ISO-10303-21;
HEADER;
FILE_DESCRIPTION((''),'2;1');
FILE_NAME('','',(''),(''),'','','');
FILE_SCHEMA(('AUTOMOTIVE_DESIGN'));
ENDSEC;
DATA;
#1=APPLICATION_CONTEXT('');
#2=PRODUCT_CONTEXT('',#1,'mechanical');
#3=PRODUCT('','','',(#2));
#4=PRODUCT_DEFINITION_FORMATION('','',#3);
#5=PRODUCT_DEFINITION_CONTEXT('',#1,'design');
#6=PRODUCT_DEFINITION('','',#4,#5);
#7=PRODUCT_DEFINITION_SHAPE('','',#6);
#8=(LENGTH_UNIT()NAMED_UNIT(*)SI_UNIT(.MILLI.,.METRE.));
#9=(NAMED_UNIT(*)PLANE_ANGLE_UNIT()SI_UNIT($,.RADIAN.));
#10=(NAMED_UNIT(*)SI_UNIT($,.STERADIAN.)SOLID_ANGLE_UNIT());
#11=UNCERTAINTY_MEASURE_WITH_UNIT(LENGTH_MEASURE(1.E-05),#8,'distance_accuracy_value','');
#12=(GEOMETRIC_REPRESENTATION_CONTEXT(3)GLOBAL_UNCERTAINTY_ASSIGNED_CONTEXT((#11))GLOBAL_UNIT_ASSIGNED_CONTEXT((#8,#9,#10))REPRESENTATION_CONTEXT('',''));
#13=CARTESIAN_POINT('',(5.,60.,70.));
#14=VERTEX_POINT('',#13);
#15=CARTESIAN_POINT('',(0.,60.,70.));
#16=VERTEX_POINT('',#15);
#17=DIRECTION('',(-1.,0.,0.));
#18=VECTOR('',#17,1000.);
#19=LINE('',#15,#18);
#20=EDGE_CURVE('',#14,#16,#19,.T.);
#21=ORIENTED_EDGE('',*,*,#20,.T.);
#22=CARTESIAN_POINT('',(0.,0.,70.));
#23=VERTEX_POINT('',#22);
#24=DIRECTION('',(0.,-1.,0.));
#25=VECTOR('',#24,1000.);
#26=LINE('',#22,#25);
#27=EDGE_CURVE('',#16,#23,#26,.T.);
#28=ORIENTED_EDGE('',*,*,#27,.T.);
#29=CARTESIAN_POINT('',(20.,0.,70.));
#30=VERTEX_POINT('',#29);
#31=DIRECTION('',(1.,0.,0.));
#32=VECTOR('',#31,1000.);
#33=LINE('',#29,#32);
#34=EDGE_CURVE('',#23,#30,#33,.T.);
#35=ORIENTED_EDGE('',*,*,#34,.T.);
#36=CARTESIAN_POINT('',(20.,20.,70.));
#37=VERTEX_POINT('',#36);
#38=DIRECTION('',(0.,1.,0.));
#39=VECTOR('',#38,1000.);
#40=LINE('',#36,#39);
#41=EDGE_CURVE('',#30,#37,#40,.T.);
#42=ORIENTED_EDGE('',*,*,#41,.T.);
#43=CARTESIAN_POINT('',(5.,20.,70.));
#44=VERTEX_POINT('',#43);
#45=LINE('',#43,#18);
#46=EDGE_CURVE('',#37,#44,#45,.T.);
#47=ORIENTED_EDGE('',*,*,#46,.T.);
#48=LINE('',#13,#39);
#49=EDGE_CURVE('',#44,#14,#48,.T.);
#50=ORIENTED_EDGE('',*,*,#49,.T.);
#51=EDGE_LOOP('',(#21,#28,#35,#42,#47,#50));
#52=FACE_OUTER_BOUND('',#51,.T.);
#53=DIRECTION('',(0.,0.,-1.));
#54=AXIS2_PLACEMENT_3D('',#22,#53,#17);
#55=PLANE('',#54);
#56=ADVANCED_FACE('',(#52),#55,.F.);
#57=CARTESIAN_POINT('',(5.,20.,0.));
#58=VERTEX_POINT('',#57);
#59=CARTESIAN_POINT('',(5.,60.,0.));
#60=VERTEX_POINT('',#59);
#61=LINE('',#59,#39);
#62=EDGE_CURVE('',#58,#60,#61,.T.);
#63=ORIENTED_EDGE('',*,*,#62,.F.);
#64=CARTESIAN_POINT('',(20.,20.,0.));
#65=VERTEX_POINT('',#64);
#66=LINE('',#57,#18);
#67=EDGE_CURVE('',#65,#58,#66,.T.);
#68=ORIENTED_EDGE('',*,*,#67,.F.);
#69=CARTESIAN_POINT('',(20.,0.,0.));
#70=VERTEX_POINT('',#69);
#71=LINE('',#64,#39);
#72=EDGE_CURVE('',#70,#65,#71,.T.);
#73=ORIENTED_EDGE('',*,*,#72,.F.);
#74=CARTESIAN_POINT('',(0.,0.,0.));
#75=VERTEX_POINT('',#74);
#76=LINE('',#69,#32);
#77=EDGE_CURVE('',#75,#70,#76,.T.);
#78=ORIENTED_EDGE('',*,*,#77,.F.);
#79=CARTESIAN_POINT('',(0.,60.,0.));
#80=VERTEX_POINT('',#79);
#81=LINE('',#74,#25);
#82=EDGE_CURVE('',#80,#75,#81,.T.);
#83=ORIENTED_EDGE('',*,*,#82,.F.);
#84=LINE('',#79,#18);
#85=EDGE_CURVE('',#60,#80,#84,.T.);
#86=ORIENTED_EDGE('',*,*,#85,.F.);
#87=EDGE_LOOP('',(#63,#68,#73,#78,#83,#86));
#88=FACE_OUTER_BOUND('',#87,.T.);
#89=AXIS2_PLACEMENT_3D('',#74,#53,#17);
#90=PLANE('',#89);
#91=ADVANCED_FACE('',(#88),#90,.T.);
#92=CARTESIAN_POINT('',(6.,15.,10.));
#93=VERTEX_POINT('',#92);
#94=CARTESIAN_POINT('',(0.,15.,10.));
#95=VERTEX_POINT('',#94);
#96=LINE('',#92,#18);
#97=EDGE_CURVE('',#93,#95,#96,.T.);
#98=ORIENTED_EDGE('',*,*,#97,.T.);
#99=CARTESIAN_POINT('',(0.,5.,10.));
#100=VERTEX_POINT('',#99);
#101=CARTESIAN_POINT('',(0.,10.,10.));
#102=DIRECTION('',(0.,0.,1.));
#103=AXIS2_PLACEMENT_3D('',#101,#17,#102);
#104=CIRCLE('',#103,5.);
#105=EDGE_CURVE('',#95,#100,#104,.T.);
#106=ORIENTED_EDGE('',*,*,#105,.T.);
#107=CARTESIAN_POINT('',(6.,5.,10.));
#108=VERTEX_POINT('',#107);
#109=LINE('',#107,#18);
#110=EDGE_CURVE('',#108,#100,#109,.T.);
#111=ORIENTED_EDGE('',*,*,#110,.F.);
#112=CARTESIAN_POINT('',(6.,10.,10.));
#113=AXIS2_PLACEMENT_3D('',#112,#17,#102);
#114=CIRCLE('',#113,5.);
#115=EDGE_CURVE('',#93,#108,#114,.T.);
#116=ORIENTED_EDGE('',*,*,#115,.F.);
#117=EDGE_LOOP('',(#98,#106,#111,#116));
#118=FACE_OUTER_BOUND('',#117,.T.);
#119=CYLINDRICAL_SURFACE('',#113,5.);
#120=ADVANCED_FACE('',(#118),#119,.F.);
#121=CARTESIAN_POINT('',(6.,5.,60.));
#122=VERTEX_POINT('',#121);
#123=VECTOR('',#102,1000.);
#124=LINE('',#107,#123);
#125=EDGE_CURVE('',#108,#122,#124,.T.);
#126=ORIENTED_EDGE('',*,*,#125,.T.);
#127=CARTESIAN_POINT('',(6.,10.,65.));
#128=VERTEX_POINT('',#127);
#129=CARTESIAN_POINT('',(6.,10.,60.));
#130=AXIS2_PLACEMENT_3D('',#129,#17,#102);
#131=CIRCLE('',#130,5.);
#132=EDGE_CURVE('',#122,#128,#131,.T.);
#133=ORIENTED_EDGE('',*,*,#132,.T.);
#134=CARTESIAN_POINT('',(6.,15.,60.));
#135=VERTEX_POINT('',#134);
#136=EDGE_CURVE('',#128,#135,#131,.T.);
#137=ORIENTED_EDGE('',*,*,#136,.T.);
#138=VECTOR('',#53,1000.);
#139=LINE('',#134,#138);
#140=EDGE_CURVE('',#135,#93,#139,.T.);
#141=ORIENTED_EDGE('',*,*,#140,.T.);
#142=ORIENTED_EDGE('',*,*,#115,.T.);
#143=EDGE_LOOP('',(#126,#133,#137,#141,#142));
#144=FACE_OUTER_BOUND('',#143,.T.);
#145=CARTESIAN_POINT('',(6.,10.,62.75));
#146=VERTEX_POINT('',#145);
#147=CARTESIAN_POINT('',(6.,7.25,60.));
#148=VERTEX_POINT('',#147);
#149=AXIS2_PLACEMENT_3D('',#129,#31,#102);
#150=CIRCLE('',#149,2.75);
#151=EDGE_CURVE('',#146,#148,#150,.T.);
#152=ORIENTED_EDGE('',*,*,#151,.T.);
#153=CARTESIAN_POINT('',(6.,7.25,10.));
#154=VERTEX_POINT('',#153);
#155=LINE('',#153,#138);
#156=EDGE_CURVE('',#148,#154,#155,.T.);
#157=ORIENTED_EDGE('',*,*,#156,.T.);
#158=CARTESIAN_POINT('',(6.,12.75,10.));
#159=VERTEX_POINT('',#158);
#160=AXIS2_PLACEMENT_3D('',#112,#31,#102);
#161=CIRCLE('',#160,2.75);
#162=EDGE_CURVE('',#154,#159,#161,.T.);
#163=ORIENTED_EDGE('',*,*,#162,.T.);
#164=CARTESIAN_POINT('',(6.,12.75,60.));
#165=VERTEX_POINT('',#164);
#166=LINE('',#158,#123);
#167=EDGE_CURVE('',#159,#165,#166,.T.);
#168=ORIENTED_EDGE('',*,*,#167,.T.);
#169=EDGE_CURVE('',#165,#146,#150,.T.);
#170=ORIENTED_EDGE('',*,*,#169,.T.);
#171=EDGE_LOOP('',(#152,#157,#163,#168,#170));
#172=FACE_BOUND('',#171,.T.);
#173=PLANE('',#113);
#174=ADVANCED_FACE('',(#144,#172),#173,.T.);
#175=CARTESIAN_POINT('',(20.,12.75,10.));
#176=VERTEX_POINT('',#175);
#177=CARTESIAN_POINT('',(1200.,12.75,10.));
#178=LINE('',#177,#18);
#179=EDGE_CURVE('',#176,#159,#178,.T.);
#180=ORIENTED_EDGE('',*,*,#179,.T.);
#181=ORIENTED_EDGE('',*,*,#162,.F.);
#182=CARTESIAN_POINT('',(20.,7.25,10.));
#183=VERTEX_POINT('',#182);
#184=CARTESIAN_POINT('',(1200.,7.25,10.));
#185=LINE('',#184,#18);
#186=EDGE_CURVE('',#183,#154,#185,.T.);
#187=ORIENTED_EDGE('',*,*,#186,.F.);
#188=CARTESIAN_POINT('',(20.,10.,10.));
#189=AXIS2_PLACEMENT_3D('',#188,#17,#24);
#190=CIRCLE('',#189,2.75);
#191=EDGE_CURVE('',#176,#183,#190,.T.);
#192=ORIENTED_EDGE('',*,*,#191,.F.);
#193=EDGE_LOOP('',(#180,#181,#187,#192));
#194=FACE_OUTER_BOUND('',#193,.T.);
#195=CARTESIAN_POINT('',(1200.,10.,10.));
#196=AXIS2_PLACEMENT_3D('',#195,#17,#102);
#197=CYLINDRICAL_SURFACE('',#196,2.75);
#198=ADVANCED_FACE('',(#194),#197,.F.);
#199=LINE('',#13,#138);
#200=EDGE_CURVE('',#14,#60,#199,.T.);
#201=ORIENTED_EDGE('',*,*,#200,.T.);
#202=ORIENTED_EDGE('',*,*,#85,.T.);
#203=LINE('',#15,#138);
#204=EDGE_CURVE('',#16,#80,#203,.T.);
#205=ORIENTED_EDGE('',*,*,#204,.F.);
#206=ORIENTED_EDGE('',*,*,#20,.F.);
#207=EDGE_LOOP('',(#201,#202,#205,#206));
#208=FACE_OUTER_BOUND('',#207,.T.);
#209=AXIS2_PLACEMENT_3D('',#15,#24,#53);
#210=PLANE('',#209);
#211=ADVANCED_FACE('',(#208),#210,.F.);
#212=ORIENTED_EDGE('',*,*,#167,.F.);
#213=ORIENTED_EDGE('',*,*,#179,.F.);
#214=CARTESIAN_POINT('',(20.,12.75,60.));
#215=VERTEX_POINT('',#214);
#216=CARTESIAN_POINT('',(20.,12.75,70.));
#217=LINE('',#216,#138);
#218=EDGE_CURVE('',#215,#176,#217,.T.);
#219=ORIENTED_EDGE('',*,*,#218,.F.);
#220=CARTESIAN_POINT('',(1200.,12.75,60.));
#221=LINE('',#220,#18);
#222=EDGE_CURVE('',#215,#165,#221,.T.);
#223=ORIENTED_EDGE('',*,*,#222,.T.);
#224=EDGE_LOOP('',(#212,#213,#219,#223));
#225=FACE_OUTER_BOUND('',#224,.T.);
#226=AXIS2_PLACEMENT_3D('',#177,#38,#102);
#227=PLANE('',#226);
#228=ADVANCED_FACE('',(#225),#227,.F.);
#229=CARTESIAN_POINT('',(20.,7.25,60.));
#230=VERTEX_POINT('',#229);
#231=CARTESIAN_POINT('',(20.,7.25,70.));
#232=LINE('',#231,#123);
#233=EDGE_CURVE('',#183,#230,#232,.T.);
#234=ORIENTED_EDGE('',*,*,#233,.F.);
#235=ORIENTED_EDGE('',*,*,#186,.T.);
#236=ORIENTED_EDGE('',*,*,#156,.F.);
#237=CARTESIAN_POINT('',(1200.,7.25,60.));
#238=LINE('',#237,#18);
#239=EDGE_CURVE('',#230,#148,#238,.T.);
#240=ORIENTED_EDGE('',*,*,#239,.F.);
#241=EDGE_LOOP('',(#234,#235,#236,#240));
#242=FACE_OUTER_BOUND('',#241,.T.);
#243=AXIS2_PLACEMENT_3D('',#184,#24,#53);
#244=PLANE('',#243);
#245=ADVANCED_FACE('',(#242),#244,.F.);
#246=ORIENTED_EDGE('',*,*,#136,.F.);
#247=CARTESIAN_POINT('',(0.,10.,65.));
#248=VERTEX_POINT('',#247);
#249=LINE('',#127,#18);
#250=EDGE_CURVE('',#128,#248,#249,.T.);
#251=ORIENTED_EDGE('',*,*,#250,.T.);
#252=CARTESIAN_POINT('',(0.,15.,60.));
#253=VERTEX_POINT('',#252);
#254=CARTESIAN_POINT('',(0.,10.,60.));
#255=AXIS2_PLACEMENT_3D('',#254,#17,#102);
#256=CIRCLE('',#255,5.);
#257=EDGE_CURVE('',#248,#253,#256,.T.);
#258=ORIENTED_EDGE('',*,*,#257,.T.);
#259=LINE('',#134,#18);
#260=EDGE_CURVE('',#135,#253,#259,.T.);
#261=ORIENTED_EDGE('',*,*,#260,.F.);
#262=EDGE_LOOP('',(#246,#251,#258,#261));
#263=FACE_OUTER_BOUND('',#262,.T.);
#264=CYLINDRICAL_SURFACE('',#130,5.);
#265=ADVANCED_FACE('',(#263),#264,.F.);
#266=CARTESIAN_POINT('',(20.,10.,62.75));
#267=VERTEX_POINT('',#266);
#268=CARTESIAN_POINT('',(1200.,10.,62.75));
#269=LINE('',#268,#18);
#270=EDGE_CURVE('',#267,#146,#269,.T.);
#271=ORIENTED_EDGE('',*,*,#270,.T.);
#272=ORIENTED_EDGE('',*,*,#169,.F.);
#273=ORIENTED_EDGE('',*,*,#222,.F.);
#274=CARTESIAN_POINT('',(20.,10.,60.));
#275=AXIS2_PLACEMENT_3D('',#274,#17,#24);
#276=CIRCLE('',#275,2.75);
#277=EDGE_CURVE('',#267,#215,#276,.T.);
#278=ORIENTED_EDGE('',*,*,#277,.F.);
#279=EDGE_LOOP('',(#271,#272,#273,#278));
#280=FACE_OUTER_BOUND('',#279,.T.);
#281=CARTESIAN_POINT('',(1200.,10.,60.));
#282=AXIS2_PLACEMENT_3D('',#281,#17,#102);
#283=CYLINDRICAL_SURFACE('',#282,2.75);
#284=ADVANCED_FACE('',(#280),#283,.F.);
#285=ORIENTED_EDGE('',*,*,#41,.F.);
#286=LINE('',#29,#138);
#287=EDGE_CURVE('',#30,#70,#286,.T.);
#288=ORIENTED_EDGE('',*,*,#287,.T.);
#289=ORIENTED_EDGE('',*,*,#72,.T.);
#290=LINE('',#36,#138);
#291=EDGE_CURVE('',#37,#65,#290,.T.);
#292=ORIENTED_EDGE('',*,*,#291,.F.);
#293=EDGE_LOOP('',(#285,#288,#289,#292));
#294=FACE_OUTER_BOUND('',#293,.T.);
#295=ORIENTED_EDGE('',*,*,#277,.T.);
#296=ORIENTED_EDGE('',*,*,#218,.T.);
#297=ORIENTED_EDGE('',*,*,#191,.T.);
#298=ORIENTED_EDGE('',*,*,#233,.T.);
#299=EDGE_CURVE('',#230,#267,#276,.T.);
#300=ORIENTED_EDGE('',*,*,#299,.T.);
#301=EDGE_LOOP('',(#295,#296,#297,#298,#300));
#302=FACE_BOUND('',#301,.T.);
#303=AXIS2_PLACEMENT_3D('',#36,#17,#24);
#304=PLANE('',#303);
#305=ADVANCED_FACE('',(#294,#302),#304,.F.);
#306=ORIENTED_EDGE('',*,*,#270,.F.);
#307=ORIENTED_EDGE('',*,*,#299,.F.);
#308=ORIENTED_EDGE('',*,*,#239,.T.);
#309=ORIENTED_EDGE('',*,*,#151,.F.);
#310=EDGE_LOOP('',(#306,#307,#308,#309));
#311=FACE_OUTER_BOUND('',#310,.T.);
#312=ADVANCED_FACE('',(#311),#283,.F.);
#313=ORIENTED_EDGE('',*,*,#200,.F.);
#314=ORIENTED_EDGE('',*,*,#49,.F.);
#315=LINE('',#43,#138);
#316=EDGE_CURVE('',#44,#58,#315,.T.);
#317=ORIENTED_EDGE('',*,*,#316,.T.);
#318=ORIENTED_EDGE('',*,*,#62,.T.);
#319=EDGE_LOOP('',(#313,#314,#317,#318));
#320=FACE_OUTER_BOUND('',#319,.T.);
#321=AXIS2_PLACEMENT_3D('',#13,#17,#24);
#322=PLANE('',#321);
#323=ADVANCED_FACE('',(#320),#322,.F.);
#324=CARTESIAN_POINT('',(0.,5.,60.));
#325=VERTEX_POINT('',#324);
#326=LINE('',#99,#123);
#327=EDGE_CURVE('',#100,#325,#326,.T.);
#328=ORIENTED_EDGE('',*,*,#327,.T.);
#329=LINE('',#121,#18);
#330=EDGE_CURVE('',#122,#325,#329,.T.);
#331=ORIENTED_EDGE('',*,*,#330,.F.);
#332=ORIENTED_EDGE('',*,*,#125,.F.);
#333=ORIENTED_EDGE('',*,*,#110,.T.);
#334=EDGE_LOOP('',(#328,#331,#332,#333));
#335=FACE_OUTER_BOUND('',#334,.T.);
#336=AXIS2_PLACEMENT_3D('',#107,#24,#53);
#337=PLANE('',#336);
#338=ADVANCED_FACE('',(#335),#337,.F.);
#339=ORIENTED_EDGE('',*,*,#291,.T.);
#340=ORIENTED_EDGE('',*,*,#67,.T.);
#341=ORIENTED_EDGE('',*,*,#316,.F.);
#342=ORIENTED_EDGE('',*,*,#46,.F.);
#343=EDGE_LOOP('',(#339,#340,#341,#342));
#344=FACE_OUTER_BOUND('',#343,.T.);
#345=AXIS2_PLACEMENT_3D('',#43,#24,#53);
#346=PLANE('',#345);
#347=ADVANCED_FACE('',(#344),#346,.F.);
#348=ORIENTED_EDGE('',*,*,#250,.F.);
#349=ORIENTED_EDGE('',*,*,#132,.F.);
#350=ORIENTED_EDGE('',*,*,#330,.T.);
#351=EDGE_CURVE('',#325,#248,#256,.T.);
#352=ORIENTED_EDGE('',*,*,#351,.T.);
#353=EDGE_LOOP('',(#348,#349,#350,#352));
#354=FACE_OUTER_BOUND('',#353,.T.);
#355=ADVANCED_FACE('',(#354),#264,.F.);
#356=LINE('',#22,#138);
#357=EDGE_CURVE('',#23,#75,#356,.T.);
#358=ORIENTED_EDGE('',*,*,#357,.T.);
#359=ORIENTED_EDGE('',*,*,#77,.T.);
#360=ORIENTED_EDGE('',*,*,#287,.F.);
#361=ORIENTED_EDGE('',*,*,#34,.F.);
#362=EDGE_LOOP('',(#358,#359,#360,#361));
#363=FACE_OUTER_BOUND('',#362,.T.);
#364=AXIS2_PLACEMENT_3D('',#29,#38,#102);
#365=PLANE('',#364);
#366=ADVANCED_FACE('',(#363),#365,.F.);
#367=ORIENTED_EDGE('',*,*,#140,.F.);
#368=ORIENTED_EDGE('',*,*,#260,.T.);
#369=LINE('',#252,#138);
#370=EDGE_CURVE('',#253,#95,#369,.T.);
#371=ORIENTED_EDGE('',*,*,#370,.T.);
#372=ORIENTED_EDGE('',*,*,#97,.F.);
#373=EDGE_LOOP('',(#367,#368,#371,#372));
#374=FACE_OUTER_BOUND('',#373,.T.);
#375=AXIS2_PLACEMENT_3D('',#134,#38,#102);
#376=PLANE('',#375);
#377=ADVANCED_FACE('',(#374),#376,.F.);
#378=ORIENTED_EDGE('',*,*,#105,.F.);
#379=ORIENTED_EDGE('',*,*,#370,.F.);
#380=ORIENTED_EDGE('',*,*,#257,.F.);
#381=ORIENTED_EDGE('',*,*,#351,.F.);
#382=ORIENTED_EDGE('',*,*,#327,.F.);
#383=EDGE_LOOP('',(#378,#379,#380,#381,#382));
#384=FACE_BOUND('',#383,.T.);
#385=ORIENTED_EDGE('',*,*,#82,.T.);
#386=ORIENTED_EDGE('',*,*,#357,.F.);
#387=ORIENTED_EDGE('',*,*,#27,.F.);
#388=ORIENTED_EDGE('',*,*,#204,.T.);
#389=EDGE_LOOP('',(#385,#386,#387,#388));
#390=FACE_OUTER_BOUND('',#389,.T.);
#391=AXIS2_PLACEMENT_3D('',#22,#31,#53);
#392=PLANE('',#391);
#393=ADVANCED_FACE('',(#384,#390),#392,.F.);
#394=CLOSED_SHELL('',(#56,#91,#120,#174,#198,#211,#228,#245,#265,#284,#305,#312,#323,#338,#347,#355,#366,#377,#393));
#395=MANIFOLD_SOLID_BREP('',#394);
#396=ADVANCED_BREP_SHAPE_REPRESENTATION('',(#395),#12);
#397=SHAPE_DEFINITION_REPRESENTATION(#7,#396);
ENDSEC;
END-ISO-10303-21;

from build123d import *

# Parameters (mm, degrees)
EXTRUDE_1_DEPTH     = 70
CUT_EXTRUDE_1_DEPTH = 1200
CUT_EXTRUDE_2_DEPTH = 6


with BuildPart() as part:
    # 草图1 → 凸台-拉伸1 (new body)
    with BuildSketch(Plane.XY):
        Polygon((0, 0), (0, 60), (5, 60), (5, 20), (20, 20), (20, 0), align=None)
    extrude(amount=EXTRUDE_1_DEPTH)

    # 草图3 → 切除-拉伸1 (cut)
    with BuildSketch(Plane.ZY):
        with BuildLine():
            Line((10, 12.75), (60, 12.75))
            ThreePointArc((60, 12.75), (62.75, 10), (60, 7.25))
            Line((60, 7.25), (10, 7.25))
            ThreePointArc((10, 7.25), (7.25, 10), (10, 12.75))
        make_face()
    extrude(amount=-CUT_EXTRUDE_1_DEPTH, mode=Mode.SUBTRACT)

    # 草图6 → 切除-拉伸2 (cut)
    with BuildSketch(Plane.ZY):
        with BuildLine():
            Line((10, 5), (60, 5))
            ThreePointArc((60, 5), (65, 10), (60, 15))
            Line((60, 15), (10, 15))
            ThreePointArc((10, 15), (5, 10), (10, 5))
        make_face()
    extrude(amount=-CUT_EXTRUDE_2_DEPTH, mode=Mode.SUBTRACT)


solid = part.part
